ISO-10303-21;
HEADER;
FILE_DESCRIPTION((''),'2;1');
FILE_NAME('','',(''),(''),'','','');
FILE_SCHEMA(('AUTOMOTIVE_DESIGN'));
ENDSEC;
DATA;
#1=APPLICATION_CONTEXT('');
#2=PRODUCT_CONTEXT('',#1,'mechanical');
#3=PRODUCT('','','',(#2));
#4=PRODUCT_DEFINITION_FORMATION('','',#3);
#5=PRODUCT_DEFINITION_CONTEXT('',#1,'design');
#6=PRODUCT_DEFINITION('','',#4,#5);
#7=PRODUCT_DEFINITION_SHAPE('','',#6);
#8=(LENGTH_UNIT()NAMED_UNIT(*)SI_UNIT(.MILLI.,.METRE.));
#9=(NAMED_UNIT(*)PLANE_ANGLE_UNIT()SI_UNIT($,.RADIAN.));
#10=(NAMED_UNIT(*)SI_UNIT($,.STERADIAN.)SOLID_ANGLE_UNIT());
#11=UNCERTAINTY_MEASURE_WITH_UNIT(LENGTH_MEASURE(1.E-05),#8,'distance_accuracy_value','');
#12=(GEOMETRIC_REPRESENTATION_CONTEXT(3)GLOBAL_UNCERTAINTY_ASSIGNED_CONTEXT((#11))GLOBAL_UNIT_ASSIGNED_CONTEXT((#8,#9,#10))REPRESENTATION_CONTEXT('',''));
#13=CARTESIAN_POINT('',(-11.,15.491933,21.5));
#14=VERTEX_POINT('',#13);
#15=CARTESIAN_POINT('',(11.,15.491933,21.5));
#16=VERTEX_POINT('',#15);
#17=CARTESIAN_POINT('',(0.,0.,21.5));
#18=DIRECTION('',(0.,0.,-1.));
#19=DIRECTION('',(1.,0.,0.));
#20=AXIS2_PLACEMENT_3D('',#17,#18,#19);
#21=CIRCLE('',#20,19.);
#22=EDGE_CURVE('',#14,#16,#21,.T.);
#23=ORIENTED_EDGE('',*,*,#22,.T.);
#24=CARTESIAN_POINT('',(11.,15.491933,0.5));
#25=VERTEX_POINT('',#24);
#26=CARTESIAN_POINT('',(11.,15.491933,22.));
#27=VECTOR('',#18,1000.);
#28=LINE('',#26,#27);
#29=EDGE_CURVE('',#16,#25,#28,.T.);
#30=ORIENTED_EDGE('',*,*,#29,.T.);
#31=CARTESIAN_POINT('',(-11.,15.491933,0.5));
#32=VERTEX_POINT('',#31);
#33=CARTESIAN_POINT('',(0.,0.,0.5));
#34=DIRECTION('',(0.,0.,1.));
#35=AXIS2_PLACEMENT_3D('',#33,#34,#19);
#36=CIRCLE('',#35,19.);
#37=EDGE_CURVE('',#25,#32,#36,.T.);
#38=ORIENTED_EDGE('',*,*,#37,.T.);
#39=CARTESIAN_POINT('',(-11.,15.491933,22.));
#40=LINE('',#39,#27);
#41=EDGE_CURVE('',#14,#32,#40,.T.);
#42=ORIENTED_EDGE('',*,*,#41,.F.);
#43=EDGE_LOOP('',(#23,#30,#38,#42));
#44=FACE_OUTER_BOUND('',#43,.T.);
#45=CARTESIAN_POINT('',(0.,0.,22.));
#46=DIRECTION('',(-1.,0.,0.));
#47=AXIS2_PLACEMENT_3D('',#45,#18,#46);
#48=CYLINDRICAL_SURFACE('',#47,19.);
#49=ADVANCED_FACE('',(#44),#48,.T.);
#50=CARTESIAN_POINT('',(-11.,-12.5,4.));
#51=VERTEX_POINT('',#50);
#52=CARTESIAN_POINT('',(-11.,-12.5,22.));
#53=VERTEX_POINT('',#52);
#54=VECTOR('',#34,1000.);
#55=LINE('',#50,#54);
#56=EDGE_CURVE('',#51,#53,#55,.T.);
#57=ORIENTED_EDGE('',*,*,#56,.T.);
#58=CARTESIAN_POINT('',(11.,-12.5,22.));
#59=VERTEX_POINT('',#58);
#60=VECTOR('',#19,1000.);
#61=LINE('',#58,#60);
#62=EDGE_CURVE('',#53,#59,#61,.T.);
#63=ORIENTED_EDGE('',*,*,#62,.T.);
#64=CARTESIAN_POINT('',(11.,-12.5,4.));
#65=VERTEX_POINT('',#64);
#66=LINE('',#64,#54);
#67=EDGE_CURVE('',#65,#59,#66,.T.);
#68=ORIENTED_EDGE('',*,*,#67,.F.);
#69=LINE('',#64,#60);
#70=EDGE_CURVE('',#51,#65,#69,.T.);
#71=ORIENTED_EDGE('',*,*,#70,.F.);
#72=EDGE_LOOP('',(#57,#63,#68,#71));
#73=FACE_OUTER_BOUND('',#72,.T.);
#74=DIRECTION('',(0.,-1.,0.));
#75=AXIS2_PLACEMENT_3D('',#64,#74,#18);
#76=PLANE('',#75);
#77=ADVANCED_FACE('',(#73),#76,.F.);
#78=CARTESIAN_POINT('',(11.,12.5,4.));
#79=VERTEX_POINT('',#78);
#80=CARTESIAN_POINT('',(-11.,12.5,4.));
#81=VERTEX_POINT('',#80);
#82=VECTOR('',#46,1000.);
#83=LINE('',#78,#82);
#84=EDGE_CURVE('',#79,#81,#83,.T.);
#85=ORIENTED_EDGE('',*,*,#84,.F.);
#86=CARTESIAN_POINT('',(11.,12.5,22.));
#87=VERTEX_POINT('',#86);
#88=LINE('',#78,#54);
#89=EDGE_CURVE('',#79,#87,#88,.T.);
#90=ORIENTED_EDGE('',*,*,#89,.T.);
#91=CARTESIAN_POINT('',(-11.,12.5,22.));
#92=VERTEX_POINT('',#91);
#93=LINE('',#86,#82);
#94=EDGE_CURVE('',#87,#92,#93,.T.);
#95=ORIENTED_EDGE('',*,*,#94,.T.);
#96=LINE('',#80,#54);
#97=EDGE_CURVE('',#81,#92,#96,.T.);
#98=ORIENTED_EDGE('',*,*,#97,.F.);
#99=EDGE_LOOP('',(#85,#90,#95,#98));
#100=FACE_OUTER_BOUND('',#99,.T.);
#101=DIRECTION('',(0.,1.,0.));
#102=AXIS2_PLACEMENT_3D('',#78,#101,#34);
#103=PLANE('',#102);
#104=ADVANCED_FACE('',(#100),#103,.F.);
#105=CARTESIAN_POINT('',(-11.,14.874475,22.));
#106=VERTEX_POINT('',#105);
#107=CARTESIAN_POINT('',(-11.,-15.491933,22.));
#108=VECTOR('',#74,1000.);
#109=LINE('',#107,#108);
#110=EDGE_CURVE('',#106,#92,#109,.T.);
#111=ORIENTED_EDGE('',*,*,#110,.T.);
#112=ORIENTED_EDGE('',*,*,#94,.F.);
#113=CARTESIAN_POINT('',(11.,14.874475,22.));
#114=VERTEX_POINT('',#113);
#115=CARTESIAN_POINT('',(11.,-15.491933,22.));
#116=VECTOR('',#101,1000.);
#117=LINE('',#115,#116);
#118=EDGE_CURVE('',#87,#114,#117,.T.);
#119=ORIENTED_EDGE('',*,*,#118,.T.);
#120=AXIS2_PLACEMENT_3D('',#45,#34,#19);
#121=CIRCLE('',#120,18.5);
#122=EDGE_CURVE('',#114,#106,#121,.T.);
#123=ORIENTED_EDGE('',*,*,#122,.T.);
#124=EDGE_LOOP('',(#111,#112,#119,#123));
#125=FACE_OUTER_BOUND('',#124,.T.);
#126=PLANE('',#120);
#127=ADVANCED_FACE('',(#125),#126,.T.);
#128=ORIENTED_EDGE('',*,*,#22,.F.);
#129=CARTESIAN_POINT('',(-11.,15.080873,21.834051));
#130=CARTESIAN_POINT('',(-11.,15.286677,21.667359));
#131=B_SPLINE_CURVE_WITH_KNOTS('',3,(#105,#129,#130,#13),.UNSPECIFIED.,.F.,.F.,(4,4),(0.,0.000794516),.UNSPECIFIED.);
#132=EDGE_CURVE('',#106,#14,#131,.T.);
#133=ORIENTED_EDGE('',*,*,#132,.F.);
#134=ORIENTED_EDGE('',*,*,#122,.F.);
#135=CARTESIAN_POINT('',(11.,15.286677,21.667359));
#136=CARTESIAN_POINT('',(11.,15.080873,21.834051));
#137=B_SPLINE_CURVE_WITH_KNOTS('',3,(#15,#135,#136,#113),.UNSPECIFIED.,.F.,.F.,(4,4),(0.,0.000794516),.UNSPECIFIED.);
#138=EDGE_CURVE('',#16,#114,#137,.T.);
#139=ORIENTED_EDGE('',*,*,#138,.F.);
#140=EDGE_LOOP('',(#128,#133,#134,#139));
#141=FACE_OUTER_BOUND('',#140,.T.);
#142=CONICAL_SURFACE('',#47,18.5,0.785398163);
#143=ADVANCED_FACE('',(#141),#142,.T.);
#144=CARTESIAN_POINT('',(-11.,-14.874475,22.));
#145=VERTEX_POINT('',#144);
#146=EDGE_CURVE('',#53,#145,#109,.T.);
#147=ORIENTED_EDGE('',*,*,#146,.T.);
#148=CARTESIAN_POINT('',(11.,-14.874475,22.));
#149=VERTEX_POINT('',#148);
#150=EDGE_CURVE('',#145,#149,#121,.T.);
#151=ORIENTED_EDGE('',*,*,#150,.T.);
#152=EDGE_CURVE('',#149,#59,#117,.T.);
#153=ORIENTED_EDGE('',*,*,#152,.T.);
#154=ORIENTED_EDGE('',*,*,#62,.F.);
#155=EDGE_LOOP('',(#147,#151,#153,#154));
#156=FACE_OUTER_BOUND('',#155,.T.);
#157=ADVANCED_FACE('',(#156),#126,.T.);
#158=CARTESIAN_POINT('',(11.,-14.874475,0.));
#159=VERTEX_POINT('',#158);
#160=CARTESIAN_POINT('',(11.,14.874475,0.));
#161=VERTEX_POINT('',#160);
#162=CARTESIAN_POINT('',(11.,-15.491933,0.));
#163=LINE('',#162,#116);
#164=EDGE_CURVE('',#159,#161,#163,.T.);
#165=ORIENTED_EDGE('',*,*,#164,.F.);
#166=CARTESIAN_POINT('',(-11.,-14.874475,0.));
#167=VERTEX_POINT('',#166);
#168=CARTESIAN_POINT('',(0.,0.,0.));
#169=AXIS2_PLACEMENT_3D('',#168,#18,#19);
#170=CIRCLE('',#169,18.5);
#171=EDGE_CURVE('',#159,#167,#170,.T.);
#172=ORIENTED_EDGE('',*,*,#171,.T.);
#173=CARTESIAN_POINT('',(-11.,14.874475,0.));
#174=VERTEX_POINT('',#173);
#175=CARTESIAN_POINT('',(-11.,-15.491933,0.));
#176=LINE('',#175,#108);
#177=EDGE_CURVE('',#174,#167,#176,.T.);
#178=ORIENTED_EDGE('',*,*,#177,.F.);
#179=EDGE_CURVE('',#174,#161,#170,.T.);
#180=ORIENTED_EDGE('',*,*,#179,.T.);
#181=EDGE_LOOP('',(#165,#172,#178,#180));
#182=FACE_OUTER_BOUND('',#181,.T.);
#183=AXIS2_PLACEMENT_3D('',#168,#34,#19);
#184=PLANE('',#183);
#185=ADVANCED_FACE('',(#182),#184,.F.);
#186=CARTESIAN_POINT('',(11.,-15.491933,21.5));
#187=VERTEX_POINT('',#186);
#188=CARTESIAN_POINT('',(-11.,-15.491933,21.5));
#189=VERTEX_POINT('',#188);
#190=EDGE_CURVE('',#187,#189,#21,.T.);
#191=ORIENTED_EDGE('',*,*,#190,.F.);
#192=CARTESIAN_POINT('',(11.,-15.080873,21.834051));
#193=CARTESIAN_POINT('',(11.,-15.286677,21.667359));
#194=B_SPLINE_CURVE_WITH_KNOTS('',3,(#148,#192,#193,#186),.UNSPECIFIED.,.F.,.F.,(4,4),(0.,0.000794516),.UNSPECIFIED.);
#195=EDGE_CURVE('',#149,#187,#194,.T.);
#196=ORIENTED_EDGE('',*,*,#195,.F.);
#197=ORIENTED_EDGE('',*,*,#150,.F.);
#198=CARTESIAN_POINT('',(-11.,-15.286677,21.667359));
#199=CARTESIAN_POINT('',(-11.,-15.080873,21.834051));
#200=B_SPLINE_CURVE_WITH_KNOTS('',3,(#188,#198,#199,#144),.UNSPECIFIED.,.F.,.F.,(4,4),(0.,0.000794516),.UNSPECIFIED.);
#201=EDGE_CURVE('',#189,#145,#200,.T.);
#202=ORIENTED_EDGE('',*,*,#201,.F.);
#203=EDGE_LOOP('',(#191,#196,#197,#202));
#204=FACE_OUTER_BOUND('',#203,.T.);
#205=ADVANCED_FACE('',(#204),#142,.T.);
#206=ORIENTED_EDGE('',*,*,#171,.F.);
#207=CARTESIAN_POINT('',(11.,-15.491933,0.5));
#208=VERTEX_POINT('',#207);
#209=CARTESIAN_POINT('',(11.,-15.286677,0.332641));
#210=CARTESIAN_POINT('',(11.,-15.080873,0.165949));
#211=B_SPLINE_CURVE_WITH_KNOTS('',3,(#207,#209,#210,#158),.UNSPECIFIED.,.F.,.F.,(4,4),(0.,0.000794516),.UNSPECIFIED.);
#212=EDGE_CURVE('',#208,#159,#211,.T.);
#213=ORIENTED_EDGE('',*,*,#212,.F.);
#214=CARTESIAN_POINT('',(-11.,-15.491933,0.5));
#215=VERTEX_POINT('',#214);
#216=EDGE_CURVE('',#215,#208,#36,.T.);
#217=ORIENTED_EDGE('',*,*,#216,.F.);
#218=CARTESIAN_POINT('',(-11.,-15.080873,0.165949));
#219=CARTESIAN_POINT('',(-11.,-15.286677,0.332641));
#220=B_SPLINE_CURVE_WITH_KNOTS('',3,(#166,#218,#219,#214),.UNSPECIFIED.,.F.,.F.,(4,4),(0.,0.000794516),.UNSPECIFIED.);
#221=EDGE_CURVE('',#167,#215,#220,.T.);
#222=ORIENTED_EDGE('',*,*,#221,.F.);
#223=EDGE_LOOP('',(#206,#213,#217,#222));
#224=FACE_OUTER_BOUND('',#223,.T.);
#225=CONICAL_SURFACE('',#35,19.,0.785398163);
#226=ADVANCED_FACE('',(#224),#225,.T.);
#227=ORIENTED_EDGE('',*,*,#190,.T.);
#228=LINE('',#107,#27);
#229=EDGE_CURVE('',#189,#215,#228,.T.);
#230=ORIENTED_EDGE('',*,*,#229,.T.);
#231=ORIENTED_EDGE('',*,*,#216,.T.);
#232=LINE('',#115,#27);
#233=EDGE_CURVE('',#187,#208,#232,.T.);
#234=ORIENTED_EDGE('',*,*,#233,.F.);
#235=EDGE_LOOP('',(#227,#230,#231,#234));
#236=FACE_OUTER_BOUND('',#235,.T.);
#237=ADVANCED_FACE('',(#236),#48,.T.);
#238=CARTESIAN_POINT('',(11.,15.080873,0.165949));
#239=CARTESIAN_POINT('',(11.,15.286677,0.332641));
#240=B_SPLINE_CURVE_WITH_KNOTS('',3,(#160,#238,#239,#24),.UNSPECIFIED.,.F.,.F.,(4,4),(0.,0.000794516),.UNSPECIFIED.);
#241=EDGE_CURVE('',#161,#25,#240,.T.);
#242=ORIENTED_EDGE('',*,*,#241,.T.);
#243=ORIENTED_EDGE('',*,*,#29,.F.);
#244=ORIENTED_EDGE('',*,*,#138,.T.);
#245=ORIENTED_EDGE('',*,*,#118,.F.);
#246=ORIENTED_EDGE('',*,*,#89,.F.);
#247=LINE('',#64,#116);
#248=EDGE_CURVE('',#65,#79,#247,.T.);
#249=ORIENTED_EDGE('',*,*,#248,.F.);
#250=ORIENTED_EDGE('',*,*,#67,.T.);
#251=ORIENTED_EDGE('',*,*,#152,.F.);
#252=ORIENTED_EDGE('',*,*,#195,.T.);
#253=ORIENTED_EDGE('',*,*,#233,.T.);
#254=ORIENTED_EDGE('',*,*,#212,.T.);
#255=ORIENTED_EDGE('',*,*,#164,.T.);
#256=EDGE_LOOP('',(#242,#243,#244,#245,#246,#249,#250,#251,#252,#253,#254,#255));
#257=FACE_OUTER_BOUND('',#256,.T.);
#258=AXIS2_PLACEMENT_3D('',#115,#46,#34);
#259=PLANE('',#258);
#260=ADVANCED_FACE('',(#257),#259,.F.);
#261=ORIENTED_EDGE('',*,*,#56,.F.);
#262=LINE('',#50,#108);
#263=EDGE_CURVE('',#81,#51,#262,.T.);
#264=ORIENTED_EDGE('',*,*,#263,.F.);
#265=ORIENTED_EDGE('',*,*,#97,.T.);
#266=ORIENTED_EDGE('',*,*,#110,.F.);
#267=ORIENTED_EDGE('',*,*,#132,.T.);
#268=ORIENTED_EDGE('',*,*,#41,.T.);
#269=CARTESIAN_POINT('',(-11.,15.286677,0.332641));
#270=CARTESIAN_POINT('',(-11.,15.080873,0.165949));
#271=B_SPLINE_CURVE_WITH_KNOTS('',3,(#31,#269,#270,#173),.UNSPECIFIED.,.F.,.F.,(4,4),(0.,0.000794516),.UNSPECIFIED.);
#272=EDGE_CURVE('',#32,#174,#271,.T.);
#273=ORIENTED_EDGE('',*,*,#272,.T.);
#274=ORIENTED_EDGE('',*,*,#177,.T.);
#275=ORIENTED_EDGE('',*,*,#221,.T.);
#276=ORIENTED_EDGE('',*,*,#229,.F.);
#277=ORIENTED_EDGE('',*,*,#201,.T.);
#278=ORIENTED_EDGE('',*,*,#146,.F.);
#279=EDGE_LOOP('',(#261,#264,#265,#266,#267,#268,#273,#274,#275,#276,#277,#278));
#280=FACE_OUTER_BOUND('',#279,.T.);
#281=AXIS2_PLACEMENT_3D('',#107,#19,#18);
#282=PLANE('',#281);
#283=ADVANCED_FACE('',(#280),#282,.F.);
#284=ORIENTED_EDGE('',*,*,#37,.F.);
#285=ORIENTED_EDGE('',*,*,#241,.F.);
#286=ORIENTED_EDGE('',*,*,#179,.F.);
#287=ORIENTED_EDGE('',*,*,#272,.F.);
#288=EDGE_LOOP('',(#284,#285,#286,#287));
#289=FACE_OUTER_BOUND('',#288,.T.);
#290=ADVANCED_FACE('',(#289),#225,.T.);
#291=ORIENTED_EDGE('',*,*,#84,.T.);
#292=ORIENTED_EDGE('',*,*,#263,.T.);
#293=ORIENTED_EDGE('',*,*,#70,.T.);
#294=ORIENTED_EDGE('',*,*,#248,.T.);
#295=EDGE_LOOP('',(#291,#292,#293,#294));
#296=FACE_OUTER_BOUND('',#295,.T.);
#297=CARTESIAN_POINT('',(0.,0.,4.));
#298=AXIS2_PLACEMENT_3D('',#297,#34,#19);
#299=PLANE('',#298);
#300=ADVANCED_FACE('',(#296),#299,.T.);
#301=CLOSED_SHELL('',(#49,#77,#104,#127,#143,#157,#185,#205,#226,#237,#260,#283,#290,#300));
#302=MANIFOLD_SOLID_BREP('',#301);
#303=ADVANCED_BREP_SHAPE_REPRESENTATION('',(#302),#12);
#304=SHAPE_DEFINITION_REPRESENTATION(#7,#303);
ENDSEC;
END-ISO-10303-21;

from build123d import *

# Parameters (mm, degrees)
BOSS_EXTRUDE1_DEPTH = 22
SKETCH2_W           = 22
SKETCH2_H           = 25
CUT_EXTRUDE1_DEPTH  = 18
CHAMFER1_SIZE       = 0.5


with BuildPart() as part:
    # Sketch1 → Boss-Extrude1 (new body)
    with BuildSketch(Plane.XY):
        with BuildLine():
            Line((11, -15.491933385), (11, 15.491933385))
            ThreePointArc((11, 15.491933385), (0, 19), (-11, 15.491933385))
            Line((-11, 15.491933385), (-11, -15.491933385))
            ThreePointArc((-11, -15.491933385), (0, -19), (11, -15.491933385))
        make_face()
    extrude(amount=BOSS_EXTRUDE1_DEPTH)

    # Sketch2 → Cut-Extrude1 (cut)
    with BuildSketch(Plane.XY.offset(22)):
        Rectangle(SKETCH2_W, SKETCH2_H)
    extrude(amount=-CUT_EXTRUDE1_DEPTH, mode=Mode.SUBTRACT)

    # Chamfer1
    chamfer1_edges = [part.edges().sort_by_distance(p)[0] for p in [
        (0, 19, 22),
        (0, -19, 22),
        (0, 19, 0),
        (0, -19, 0),
    ]]
    chamfer(chamfer1_edges, length=CHAMFER1_SIZE)


solid = part.part
